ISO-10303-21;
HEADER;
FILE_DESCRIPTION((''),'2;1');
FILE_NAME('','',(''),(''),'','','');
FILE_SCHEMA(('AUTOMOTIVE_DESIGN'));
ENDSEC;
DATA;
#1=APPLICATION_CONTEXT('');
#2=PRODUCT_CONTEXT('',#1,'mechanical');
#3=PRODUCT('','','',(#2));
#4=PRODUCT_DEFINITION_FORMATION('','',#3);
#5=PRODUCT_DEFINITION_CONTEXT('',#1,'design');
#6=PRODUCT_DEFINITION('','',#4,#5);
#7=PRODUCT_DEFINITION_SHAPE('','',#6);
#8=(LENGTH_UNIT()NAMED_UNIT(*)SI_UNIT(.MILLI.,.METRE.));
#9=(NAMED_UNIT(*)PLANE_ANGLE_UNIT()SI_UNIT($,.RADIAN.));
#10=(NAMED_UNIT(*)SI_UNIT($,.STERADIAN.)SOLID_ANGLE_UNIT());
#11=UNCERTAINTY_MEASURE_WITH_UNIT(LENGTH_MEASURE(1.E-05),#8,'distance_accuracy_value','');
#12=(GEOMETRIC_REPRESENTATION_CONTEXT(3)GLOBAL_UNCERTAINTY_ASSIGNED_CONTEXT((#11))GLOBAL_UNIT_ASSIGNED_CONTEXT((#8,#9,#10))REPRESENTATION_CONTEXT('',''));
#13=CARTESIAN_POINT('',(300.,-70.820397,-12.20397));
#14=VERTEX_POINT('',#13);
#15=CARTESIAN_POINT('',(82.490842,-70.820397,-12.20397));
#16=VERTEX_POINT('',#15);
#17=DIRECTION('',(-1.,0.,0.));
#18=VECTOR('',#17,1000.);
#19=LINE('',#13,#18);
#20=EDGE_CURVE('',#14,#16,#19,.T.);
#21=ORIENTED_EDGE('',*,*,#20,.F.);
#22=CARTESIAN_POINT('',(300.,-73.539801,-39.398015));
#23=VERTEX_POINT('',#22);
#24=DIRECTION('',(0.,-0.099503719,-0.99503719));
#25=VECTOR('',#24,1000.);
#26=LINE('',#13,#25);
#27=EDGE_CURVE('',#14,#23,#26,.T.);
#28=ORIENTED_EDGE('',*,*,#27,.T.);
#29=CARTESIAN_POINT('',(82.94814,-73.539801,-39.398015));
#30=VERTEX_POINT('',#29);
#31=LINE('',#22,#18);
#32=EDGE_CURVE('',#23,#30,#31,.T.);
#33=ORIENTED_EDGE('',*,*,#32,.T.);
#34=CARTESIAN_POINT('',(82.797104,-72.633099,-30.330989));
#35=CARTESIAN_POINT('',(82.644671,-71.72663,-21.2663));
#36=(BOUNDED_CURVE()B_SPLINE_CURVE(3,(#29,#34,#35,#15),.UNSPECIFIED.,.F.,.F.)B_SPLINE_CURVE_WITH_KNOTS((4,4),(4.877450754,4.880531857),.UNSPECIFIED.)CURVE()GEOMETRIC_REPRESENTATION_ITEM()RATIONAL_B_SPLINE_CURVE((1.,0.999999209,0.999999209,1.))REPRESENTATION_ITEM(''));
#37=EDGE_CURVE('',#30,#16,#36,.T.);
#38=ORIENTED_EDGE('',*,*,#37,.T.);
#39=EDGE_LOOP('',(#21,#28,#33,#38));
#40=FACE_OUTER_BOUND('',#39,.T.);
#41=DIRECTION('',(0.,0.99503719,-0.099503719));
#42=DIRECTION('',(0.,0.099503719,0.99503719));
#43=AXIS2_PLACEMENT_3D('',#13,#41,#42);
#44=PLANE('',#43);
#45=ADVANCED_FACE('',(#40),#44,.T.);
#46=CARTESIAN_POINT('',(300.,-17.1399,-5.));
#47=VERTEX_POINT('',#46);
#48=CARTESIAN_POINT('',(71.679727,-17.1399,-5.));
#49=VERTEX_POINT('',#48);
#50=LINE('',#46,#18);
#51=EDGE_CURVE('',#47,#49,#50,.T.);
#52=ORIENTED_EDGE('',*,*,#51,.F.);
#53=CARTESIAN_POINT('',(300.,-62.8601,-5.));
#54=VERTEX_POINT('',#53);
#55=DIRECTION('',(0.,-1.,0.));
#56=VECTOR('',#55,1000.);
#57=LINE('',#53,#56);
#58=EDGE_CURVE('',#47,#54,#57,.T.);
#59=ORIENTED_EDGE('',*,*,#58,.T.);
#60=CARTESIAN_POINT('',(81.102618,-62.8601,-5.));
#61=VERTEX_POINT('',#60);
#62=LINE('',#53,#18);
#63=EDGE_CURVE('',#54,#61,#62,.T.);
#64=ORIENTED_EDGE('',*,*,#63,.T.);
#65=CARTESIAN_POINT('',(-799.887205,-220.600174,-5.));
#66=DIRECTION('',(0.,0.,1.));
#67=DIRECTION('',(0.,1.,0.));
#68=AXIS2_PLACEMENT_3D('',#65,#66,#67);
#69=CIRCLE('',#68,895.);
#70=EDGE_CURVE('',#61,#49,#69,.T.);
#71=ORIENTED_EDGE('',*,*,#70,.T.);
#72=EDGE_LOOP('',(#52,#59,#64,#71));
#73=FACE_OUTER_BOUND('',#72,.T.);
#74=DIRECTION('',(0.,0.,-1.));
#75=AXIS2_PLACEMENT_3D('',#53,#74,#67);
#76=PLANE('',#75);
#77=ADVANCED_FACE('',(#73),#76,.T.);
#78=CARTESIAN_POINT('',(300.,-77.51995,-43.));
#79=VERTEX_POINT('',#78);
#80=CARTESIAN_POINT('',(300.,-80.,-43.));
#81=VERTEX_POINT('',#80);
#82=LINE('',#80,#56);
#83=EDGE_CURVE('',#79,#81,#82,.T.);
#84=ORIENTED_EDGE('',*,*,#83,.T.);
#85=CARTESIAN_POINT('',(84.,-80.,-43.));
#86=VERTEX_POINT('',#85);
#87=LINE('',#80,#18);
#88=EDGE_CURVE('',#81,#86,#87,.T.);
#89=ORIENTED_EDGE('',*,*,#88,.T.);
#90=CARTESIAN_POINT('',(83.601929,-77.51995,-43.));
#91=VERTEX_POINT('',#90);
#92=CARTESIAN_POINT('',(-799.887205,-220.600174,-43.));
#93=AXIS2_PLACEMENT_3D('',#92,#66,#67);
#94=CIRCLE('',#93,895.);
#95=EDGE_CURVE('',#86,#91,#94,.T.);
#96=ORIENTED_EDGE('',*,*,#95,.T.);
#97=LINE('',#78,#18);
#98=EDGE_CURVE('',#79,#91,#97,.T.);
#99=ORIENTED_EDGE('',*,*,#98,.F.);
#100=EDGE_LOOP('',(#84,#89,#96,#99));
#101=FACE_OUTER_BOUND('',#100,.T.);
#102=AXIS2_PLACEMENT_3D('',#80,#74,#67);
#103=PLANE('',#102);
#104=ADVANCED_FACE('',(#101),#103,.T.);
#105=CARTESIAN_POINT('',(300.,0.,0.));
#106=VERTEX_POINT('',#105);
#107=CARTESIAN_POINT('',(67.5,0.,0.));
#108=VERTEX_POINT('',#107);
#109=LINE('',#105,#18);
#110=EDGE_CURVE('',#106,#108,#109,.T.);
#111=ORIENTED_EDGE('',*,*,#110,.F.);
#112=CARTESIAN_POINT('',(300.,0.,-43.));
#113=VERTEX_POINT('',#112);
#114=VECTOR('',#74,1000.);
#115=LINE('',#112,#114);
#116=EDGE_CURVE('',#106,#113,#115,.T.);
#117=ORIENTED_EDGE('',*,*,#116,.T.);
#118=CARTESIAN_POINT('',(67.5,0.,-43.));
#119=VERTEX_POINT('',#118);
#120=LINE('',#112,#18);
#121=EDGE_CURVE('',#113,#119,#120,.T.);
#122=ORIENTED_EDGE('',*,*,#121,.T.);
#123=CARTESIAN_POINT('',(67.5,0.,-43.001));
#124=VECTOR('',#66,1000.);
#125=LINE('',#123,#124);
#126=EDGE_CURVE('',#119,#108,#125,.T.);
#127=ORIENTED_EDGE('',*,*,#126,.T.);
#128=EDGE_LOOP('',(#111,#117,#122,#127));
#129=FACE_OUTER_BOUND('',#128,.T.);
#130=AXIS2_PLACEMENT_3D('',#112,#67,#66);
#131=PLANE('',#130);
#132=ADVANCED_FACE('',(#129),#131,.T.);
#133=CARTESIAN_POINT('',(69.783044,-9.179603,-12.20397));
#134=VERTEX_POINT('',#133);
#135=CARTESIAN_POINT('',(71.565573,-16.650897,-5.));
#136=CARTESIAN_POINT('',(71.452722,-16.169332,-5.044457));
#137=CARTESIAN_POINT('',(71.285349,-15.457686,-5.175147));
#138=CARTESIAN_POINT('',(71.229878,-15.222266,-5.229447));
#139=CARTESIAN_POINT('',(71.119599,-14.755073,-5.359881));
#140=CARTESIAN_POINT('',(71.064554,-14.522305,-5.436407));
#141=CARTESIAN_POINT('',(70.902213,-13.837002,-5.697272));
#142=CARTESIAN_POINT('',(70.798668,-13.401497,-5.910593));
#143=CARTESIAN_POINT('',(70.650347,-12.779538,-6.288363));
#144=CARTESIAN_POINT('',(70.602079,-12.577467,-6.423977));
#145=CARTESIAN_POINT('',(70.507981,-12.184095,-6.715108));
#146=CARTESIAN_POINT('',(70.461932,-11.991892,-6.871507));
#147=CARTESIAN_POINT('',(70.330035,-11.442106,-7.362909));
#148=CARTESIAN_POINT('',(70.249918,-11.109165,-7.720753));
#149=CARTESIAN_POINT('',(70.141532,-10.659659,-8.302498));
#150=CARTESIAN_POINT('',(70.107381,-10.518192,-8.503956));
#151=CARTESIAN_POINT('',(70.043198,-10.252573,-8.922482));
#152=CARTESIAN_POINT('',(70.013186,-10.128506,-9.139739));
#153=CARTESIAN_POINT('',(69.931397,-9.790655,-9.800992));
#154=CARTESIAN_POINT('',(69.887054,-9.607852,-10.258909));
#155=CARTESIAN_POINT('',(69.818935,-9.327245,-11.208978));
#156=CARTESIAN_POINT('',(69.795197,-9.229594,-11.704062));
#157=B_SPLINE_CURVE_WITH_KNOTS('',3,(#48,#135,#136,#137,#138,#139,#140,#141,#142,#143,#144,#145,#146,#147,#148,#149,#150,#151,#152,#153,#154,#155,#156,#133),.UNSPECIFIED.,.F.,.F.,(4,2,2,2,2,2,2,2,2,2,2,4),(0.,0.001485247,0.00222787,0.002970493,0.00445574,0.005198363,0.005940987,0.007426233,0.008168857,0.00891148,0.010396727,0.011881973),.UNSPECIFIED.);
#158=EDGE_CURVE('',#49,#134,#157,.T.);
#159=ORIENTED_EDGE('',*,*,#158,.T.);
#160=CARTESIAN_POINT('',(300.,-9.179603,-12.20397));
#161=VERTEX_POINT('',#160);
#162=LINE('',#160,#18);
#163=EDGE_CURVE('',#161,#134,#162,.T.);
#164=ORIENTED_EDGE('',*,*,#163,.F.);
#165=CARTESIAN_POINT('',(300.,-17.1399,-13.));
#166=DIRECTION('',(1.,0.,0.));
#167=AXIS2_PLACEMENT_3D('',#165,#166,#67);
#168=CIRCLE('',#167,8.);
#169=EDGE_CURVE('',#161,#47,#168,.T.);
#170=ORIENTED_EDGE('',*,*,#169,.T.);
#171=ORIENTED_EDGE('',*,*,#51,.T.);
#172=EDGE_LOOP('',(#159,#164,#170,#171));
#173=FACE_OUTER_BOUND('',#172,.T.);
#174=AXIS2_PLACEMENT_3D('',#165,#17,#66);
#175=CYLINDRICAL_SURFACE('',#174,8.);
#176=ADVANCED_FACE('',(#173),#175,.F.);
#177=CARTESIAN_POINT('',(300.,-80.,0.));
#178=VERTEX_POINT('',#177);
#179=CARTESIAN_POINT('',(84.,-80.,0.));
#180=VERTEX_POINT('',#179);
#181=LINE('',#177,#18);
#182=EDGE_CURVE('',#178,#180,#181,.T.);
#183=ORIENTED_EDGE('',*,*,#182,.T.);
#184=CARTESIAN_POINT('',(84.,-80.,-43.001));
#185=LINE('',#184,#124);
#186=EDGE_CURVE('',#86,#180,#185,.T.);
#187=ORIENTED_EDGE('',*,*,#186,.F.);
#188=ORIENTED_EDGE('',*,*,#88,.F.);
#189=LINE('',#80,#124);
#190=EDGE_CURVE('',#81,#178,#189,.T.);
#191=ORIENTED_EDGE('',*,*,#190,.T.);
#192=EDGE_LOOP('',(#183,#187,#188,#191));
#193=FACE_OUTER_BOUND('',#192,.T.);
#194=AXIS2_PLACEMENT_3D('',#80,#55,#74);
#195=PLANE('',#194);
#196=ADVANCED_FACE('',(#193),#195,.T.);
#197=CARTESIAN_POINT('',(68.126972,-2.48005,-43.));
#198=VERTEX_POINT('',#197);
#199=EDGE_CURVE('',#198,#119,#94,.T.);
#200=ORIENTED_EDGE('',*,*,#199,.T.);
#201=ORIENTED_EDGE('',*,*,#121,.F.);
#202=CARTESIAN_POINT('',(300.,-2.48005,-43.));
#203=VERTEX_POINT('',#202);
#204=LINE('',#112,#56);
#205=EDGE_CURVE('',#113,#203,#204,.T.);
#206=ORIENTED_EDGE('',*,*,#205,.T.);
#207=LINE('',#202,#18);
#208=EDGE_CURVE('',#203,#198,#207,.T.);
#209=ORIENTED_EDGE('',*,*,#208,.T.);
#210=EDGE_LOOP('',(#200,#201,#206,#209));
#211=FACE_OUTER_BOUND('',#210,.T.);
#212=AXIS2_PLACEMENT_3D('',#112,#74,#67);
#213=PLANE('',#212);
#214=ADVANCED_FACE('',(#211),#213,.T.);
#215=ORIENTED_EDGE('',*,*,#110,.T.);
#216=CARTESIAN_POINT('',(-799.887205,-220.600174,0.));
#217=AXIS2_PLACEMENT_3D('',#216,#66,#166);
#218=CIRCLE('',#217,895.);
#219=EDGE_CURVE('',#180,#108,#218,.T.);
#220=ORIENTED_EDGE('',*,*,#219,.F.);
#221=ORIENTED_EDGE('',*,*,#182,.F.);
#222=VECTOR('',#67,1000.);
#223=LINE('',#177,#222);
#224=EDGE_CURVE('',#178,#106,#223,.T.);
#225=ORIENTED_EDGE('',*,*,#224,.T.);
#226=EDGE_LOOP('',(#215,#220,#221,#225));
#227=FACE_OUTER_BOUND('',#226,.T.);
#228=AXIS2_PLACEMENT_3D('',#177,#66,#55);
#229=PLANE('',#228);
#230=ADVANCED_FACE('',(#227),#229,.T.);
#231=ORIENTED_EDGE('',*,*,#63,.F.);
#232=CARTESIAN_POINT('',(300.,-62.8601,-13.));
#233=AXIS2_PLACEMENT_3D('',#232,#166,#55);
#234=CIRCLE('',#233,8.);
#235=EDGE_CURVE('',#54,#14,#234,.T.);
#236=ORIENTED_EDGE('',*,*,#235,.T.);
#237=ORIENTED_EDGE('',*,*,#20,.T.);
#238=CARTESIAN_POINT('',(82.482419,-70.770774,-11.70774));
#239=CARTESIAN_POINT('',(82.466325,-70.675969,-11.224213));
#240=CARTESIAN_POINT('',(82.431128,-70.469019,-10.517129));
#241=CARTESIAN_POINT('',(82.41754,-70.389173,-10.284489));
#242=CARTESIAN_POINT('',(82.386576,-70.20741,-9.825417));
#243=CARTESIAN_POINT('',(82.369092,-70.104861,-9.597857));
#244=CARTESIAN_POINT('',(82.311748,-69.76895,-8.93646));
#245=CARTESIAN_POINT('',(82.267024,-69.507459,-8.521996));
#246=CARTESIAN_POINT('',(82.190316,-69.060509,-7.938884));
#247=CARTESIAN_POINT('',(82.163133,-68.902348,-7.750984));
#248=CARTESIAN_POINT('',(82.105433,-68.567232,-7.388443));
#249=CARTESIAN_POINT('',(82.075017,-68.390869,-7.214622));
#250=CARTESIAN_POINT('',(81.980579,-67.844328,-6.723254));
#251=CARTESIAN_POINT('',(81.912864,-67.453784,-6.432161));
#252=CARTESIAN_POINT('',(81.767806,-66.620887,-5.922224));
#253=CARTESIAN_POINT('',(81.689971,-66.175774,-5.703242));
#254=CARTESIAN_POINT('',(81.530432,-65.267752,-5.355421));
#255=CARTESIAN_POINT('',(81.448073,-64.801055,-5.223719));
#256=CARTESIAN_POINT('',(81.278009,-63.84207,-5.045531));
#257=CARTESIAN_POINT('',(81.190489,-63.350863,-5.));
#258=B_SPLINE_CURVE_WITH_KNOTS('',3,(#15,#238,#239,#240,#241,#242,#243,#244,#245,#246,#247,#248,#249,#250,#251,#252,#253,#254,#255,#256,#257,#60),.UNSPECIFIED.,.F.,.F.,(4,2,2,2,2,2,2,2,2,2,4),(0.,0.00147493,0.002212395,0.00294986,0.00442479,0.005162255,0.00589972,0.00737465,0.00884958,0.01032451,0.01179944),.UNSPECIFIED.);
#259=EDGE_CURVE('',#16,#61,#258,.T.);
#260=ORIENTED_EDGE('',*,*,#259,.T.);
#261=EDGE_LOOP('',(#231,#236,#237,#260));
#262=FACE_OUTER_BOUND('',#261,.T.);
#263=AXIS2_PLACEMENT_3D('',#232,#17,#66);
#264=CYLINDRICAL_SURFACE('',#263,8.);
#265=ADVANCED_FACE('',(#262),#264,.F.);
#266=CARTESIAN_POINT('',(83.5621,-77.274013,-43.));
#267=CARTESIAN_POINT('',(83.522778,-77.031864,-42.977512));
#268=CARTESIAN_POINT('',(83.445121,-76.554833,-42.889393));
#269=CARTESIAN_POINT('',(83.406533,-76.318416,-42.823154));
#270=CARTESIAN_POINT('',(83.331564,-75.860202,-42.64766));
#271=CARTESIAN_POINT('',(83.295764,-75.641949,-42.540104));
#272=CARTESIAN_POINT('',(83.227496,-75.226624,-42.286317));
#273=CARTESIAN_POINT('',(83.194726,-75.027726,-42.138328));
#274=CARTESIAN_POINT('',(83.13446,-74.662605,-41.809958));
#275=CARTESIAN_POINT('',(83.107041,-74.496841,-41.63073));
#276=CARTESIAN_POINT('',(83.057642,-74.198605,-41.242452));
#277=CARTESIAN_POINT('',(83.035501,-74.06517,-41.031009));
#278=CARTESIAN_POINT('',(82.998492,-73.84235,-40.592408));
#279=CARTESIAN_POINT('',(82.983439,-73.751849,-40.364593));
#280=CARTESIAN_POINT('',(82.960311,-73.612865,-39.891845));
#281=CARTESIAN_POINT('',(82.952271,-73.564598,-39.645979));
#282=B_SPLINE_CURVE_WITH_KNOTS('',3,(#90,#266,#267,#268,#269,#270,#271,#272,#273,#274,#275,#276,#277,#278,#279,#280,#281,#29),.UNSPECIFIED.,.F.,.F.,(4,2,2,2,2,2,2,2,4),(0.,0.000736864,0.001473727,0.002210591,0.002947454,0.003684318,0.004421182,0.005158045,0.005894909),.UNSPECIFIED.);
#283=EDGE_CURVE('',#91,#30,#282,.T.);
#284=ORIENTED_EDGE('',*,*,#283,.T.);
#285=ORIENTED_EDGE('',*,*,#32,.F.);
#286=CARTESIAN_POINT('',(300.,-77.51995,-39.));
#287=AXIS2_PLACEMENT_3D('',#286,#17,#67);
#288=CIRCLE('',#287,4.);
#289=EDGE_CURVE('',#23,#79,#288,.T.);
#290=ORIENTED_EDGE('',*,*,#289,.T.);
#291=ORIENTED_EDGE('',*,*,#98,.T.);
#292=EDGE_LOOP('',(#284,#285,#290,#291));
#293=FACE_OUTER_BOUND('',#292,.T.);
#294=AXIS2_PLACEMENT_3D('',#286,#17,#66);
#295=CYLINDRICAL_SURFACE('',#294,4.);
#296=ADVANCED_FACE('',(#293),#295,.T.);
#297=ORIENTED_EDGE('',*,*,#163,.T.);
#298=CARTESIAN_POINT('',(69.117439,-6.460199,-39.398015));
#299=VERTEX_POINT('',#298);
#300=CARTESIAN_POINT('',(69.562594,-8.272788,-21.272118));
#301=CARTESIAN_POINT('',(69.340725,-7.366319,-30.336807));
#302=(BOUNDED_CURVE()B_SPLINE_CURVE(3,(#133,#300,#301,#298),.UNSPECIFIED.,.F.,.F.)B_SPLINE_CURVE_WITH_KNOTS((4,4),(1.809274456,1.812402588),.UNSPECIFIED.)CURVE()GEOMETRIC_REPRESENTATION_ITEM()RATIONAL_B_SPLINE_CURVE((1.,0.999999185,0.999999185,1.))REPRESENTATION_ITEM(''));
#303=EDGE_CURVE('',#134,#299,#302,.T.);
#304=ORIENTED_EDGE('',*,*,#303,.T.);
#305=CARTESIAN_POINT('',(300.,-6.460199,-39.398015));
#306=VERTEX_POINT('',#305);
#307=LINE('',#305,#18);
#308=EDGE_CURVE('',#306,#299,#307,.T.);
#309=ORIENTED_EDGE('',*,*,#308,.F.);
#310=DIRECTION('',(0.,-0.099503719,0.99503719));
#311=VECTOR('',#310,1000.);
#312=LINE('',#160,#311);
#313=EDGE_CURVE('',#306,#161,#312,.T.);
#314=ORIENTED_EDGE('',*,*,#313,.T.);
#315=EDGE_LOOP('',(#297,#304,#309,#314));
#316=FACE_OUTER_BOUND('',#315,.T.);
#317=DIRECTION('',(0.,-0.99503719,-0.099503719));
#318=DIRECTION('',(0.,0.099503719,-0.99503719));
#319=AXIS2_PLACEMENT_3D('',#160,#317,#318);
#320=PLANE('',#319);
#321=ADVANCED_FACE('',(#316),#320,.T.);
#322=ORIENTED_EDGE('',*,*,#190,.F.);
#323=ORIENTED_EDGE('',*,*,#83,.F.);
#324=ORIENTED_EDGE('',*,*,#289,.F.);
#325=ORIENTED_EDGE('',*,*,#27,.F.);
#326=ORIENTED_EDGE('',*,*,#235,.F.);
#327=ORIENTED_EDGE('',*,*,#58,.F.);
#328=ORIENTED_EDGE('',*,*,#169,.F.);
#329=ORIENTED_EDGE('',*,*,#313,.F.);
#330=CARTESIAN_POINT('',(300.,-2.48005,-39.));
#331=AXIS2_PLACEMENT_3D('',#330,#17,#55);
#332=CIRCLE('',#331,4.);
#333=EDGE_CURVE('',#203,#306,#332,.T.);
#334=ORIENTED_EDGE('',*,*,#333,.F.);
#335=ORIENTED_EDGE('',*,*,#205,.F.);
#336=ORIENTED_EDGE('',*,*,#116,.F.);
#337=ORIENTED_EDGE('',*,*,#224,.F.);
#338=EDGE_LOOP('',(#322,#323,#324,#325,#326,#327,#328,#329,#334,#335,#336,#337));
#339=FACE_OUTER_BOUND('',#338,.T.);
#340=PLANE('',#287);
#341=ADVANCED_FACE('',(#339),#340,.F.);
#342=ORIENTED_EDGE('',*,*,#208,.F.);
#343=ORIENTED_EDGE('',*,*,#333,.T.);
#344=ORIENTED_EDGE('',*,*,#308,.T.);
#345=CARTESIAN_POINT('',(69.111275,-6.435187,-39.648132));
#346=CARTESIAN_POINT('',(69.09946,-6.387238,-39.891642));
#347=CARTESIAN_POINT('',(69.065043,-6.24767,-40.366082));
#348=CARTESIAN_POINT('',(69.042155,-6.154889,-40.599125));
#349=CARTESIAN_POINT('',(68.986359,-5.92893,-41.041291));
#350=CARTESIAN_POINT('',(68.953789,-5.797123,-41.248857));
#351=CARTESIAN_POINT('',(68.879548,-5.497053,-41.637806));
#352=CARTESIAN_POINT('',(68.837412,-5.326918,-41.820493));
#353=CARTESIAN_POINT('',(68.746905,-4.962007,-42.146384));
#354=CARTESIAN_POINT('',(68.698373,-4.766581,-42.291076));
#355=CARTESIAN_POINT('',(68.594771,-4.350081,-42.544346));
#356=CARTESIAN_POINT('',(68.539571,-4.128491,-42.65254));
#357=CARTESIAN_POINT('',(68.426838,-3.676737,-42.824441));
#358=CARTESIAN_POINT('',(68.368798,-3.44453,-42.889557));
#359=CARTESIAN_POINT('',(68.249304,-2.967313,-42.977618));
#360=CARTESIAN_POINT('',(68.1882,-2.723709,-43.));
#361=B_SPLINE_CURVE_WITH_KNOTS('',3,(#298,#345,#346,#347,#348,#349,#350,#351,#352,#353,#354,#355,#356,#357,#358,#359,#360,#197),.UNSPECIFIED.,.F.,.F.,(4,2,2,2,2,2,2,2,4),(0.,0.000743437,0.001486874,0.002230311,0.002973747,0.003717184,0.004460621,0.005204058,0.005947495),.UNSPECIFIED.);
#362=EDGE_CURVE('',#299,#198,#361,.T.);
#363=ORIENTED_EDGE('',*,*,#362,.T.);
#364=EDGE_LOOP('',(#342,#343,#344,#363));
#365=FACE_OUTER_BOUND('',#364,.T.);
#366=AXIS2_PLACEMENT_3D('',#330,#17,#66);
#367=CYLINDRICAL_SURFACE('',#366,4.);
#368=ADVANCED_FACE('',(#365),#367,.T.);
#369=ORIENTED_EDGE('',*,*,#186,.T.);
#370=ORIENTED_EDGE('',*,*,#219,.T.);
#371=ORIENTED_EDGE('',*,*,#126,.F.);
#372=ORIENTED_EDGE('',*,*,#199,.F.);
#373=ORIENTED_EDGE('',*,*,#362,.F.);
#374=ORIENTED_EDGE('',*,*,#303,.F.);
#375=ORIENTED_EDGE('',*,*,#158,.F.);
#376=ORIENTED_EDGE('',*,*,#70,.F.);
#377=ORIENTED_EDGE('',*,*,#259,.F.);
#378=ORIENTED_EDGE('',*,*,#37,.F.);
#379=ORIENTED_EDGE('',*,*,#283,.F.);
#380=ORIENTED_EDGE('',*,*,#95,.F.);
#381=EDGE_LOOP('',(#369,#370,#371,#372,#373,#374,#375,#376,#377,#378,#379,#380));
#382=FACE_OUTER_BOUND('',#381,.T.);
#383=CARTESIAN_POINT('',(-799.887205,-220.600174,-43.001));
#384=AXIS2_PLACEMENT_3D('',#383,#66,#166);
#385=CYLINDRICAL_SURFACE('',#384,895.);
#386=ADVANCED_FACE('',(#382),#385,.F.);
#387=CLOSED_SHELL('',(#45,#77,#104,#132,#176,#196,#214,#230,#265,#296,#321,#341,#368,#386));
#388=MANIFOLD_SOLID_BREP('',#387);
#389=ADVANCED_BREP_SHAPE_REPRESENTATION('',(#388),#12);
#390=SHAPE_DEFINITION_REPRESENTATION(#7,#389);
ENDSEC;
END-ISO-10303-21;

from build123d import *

# Parameters (mm, degrees)
GB_T707_1988_8_XXXXXXXXXXXXXXX528V9_1_DEPTH = 300
CUT_EXTRUDE_2_REACH                         = 315.447
SKETCH_4_R                                  = 895


with BuildPart() as part:
    # Sketch11 → 热轧普通槽钢(gb t707-1988) 8-XXXXXXXXXXXXXXX528V9(1) (new body)
    with BuildSketch(Plane(origin=(0, 0, 0), x_dir=(0, 0, -1), z_dir=(-1, 0, 0))):
        with BuildLine():
            Line((43, 80), (0, 80))
            Line((0, 80), (0, 0))
            Line((0, 0), (43, 0))
            Line((43, 0), (43, 2.480049752))
            ThreePointArc((43, 2.480049752), (41.965810134, 5.164071035), (39.398014876, 6.460198512))
            Line((39.398014876, 6.460198512), (12.203970248, 9.179602975))
            ThreePointArc((12.203970248, 9.179602975), (7.068379732, 11.771857931), (5, 17.139900497))
            Line((5, 17.139900497), (5, 62.860099503))
            ThreePointArc((5, 62.860099503), (7.068379732, 68.228142069), (12.203970248, 70.820397025))
            Line((12.203970248, 70.820397025), (39.398014876, 73.539801488))
            ThreePointArc((39.398014876, 73.539801488), (41.965810134, 74.835928965), (43, 77.519950248))
            Line((43, 77.519950248), (43, 80))
        make_face()
    extrude(amount=-GB_T707_1988_8_XXXXXXXXXXXXXXX528V9_1_DEPTH)

    # 草图4 → 切除-拉伸2 (cut, up to next)
    with BuildSketch(Plane.XY, mode=Mode.PRIVATE) as cut_extrude_2_sk1:
        with Locations((-799.887205022, -220.600173536)):
            Circle(SKETCH_4_R)
    cut_extrude_2_tool1 = extrude(cut_extrude_2_sk1.sketch, amount=-CUT_EXTRUDE_2_REACH, mode=Mode.PRIVATE) & part.part
    add(cut_extrude_2_tool1.solids().sort_by_distance((-799.887205, -220.600174, 0))[0], mode=Mode.SUBTRACT)


solid = part.part
